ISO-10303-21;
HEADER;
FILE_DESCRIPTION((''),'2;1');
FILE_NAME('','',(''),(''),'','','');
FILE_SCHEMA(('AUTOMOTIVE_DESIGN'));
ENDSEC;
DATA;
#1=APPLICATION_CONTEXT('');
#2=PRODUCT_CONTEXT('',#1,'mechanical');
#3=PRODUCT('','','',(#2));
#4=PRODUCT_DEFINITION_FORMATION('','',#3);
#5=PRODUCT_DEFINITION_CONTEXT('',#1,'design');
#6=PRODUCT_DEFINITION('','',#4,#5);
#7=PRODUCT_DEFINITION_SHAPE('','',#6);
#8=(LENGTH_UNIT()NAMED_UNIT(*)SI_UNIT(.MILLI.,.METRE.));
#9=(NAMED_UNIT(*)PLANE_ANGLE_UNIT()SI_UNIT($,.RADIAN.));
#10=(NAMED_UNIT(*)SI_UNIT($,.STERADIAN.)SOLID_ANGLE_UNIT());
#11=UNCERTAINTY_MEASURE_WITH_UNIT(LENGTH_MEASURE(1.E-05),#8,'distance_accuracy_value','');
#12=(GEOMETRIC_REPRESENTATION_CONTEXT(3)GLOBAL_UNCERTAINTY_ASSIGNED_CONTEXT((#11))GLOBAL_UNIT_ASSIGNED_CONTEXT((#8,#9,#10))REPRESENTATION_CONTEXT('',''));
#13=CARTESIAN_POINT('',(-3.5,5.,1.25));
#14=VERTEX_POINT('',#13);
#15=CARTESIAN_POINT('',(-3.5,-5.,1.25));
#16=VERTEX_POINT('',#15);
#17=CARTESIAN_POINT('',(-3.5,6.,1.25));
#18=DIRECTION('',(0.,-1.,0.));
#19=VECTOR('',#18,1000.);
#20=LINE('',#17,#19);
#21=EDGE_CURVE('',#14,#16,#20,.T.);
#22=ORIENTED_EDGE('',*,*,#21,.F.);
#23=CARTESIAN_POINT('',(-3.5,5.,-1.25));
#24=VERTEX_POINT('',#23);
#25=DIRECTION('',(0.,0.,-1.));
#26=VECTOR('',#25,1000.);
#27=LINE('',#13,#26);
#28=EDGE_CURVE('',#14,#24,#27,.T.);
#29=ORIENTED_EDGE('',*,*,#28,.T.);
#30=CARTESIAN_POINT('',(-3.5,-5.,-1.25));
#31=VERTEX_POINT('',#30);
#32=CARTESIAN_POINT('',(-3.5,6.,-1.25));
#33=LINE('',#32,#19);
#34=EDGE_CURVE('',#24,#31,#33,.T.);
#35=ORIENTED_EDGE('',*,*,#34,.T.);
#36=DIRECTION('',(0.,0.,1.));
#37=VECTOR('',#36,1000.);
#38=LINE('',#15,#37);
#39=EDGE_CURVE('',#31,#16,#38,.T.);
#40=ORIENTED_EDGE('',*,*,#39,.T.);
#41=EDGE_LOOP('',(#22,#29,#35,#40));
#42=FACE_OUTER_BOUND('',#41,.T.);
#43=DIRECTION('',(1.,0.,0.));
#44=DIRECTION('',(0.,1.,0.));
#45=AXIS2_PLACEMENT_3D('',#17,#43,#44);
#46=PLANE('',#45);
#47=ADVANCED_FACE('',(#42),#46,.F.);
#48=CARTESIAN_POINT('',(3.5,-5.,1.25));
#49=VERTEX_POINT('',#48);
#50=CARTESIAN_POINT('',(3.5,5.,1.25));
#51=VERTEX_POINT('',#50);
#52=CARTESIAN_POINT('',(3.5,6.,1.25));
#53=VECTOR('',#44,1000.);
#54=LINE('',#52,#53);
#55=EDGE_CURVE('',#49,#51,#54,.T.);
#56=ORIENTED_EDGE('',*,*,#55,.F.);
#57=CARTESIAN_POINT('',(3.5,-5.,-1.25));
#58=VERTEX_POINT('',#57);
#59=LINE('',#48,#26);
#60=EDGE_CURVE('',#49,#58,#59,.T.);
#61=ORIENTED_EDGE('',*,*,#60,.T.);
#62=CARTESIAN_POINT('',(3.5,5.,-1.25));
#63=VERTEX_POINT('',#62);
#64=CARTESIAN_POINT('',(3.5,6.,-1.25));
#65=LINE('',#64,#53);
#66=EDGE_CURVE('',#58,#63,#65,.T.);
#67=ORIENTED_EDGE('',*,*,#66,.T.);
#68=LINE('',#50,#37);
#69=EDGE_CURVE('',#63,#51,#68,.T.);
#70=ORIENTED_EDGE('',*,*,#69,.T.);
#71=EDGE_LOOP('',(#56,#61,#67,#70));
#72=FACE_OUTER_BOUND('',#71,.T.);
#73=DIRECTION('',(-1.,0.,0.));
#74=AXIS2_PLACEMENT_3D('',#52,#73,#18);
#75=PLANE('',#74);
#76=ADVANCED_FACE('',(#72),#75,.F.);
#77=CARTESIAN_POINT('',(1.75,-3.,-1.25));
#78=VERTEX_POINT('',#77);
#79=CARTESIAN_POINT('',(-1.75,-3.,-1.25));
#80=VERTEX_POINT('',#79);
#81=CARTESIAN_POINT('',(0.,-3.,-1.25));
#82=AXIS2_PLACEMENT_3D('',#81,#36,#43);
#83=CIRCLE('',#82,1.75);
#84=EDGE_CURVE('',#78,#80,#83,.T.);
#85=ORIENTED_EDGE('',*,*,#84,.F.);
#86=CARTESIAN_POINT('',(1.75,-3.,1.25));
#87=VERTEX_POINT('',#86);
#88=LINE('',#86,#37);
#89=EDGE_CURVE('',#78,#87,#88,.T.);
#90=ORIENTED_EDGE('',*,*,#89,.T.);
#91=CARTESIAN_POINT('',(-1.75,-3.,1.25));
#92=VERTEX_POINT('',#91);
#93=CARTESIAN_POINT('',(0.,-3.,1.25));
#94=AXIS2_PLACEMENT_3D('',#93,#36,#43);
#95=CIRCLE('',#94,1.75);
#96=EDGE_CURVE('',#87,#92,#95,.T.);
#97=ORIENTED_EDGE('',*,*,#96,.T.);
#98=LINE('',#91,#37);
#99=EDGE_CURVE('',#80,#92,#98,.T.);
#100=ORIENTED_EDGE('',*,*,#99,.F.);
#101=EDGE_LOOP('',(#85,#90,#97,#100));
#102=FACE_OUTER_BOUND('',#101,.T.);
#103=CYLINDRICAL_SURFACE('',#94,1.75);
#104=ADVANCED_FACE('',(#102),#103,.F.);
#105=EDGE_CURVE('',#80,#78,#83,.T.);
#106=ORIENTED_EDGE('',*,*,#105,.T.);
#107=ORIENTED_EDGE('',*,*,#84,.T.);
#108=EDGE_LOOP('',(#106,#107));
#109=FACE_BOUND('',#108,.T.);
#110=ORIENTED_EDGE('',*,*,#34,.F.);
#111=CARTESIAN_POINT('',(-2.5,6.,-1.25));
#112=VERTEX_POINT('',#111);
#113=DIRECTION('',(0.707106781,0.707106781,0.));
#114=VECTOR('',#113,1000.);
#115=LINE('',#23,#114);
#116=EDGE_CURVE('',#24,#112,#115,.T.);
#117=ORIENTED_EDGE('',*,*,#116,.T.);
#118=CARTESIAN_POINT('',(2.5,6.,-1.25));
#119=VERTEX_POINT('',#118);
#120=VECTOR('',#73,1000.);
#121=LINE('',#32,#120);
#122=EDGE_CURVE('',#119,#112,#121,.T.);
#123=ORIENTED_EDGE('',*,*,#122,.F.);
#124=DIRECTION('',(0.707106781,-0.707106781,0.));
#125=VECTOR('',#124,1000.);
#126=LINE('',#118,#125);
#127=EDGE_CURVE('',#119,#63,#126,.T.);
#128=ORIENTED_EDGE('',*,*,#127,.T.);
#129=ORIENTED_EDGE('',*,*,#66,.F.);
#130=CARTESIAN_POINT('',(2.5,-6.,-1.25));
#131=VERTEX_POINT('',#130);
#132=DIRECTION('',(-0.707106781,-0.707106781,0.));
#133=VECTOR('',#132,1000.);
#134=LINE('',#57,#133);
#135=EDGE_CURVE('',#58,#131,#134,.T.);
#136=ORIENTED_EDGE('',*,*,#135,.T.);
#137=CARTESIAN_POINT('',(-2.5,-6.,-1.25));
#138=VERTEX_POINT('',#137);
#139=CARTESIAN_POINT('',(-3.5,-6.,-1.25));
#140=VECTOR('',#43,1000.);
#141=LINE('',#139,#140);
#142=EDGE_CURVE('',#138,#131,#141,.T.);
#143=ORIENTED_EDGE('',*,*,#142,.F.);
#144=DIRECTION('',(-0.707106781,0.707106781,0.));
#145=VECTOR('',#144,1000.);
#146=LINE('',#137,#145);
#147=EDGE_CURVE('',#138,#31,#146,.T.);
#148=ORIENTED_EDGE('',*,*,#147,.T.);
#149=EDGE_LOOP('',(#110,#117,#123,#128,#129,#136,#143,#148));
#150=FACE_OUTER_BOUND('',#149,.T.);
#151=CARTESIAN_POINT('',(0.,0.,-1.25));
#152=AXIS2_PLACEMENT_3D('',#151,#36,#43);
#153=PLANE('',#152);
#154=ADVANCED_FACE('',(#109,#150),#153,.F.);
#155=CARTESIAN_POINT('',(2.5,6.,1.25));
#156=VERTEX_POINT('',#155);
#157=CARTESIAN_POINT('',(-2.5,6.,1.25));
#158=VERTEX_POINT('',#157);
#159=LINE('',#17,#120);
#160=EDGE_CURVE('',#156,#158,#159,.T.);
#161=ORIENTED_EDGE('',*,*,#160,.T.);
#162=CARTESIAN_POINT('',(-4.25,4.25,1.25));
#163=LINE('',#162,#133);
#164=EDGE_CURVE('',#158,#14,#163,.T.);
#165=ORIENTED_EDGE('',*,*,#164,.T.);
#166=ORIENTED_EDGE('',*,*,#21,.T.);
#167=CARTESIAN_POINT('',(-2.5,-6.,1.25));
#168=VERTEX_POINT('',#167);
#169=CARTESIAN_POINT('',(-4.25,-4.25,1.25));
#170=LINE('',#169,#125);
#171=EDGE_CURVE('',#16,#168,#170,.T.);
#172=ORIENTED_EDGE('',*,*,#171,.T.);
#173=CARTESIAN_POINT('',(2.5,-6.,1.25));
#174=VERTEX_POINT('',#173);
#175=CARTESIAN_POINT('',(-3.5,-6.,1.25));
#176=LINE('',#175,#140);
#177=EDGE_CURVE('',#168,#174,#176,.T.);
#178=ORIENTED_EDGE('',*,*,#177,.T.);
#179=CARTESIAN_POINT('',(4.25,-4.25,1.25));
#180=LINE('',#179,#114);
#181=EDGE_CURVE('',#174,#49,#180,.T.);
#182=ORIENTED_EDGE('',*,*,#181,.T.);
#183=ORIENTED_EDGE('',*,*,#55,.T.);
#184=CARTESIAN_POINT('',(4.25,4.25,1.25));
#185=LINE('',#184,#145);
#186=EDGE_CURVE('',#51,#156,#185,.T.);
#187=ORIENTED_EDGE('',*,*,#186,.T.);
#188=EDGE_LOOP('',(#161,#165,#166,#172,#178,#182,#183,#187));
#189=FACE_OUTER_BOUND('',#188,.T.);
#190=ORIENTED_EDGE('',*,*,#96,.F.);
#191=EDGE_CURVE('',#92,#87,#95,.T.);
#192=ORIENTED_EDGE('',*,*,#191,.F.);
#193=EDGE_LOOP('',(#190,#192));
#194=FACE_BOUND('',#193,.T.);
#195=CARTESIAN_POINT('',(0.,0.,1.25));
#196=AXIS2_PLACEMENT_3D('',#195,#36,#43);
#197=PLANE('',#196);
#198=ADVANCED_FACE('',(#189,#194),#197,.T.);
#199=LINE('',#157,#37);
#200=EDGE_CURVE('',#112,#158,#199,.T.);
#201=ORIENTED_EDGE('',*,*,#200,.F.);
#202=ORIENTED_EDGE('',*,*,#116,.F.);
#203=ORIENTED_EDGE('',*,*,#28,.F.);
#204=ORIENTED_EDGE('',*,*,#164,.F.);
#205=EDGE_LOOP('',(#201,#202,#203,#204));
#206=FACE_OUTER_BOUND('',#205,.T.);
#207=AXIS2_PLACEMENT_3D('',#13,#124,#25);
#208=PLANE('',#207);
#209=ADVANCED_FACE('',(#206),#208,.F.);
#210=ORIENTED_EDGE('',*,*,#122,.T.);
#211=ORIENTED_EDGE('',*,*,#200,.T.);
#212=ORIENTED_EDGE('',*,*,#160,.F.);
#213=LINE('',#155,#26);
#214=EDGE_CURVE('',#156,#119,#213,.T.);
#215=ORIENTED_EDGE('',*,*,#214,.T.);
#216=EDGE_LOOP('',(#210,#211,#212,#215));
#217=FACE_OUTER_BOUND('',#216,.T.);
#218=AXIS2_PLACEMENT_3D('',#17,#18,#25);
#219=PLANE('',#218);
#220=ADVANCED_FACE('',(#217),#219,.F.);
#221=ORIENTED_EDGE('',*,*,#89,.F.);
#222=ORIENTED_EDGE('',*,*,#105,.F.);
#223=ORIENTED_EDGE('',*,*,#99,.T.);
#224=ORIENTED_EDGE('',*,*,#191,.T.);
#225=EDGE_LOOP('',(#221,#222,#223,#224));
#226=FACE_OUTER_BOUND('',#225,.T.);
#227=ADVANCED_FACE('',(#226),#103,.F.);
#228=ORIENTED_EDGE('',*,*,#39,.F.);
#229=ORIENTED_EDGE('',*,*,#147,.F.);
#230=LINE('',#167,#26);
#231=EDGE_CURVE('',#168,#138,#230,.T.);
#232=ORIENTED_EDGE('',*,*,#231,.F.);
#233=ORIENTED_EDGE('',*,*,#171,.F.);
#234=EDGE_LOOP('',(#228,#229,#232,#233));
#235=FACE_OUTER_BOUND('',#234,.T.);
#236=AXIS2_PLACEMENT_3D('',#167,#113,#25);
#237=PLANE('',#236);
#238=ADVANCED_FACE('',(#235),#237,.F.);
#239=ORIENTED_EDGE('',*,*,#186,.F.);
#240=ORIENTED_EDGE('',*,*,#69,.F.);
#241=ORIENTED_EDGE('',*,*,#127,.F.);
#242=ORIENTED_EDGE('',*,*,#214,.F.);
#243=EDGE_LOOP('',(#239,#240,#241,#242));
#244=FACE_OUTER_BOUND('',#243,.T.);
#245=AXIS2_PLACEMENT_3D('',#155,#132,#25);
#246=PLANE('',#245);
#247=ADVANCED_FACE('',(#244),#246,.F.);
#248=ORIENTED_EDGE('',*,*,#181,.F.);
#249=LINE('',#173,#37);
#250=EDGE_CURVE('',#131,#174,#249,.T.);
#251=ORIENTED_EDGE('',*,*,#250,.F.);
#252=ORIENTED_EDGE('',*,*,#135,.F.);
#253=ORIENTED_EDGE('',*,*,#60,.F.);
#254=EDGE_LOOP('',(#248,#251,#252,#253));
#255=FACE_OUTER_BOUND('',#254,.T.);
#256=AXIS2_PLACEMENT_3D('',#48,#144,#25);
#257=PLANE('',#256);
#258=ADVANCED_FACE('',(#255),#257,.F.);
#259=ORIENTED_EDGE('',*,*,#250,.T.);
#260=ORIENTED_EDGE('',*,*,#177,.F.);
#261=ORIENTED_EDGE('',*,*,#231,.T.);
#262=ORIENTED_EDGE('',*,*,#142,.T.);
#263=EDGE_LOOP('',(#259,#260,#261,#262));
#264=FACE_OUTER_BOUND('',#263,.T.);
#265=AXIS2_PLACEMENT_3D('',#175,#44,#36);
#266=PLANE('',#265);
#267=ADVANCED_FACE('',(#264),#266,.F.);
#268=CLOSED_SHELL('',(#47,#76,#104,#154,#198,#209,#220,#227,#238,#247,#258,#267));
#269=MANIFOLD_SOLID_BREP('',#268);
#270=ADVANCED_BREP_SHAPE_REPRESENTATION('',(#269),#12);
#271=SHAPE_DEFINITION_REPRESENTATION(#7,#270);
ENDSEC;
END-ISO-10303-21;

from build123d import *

# Parameters (mm, degrees)
SKETCH1_W                  = 7
SKETCH1_H                  = 12
BOSS_EXTRUDE1_DEPTH        = 1.25
F_3_5_3_5_DIAMETER_HOLE1_D = 3.5
CHAMFER1_SIZE              = 1


with BuildPart() as part:
    # Sketch1 → Boss-Extrude1 (new, symmetric)
    with BuildSketch(Plane.XY):
        Rectangle(SKETCH1_W, SKETCH1_H)
    extrude(amount=BOSS_EXTRUDE1_DEPTH, both=True)

    # Ø3.5 (3.5) Diameter Hole1 (through all)
    with Locations(Plane.XY.offset(1.25)):
        with Locations((0, -3)):
            Hole(F_3_5_3_5_DIAMETER_HOLE1_D / 2)

    # Chamfer1
    chamfer1_edges = [part.edges().sort_by_distance(p)[0] for p in [
        (3.5, -6, 0),
        (-3.5, -6, 0),
        (-3.5, 6, 0),
        (3.5, 6, 0),
    ]]
    chamfer(chamfer1_edges, length=CHAMFER1_SIZE)


solid = part.part
